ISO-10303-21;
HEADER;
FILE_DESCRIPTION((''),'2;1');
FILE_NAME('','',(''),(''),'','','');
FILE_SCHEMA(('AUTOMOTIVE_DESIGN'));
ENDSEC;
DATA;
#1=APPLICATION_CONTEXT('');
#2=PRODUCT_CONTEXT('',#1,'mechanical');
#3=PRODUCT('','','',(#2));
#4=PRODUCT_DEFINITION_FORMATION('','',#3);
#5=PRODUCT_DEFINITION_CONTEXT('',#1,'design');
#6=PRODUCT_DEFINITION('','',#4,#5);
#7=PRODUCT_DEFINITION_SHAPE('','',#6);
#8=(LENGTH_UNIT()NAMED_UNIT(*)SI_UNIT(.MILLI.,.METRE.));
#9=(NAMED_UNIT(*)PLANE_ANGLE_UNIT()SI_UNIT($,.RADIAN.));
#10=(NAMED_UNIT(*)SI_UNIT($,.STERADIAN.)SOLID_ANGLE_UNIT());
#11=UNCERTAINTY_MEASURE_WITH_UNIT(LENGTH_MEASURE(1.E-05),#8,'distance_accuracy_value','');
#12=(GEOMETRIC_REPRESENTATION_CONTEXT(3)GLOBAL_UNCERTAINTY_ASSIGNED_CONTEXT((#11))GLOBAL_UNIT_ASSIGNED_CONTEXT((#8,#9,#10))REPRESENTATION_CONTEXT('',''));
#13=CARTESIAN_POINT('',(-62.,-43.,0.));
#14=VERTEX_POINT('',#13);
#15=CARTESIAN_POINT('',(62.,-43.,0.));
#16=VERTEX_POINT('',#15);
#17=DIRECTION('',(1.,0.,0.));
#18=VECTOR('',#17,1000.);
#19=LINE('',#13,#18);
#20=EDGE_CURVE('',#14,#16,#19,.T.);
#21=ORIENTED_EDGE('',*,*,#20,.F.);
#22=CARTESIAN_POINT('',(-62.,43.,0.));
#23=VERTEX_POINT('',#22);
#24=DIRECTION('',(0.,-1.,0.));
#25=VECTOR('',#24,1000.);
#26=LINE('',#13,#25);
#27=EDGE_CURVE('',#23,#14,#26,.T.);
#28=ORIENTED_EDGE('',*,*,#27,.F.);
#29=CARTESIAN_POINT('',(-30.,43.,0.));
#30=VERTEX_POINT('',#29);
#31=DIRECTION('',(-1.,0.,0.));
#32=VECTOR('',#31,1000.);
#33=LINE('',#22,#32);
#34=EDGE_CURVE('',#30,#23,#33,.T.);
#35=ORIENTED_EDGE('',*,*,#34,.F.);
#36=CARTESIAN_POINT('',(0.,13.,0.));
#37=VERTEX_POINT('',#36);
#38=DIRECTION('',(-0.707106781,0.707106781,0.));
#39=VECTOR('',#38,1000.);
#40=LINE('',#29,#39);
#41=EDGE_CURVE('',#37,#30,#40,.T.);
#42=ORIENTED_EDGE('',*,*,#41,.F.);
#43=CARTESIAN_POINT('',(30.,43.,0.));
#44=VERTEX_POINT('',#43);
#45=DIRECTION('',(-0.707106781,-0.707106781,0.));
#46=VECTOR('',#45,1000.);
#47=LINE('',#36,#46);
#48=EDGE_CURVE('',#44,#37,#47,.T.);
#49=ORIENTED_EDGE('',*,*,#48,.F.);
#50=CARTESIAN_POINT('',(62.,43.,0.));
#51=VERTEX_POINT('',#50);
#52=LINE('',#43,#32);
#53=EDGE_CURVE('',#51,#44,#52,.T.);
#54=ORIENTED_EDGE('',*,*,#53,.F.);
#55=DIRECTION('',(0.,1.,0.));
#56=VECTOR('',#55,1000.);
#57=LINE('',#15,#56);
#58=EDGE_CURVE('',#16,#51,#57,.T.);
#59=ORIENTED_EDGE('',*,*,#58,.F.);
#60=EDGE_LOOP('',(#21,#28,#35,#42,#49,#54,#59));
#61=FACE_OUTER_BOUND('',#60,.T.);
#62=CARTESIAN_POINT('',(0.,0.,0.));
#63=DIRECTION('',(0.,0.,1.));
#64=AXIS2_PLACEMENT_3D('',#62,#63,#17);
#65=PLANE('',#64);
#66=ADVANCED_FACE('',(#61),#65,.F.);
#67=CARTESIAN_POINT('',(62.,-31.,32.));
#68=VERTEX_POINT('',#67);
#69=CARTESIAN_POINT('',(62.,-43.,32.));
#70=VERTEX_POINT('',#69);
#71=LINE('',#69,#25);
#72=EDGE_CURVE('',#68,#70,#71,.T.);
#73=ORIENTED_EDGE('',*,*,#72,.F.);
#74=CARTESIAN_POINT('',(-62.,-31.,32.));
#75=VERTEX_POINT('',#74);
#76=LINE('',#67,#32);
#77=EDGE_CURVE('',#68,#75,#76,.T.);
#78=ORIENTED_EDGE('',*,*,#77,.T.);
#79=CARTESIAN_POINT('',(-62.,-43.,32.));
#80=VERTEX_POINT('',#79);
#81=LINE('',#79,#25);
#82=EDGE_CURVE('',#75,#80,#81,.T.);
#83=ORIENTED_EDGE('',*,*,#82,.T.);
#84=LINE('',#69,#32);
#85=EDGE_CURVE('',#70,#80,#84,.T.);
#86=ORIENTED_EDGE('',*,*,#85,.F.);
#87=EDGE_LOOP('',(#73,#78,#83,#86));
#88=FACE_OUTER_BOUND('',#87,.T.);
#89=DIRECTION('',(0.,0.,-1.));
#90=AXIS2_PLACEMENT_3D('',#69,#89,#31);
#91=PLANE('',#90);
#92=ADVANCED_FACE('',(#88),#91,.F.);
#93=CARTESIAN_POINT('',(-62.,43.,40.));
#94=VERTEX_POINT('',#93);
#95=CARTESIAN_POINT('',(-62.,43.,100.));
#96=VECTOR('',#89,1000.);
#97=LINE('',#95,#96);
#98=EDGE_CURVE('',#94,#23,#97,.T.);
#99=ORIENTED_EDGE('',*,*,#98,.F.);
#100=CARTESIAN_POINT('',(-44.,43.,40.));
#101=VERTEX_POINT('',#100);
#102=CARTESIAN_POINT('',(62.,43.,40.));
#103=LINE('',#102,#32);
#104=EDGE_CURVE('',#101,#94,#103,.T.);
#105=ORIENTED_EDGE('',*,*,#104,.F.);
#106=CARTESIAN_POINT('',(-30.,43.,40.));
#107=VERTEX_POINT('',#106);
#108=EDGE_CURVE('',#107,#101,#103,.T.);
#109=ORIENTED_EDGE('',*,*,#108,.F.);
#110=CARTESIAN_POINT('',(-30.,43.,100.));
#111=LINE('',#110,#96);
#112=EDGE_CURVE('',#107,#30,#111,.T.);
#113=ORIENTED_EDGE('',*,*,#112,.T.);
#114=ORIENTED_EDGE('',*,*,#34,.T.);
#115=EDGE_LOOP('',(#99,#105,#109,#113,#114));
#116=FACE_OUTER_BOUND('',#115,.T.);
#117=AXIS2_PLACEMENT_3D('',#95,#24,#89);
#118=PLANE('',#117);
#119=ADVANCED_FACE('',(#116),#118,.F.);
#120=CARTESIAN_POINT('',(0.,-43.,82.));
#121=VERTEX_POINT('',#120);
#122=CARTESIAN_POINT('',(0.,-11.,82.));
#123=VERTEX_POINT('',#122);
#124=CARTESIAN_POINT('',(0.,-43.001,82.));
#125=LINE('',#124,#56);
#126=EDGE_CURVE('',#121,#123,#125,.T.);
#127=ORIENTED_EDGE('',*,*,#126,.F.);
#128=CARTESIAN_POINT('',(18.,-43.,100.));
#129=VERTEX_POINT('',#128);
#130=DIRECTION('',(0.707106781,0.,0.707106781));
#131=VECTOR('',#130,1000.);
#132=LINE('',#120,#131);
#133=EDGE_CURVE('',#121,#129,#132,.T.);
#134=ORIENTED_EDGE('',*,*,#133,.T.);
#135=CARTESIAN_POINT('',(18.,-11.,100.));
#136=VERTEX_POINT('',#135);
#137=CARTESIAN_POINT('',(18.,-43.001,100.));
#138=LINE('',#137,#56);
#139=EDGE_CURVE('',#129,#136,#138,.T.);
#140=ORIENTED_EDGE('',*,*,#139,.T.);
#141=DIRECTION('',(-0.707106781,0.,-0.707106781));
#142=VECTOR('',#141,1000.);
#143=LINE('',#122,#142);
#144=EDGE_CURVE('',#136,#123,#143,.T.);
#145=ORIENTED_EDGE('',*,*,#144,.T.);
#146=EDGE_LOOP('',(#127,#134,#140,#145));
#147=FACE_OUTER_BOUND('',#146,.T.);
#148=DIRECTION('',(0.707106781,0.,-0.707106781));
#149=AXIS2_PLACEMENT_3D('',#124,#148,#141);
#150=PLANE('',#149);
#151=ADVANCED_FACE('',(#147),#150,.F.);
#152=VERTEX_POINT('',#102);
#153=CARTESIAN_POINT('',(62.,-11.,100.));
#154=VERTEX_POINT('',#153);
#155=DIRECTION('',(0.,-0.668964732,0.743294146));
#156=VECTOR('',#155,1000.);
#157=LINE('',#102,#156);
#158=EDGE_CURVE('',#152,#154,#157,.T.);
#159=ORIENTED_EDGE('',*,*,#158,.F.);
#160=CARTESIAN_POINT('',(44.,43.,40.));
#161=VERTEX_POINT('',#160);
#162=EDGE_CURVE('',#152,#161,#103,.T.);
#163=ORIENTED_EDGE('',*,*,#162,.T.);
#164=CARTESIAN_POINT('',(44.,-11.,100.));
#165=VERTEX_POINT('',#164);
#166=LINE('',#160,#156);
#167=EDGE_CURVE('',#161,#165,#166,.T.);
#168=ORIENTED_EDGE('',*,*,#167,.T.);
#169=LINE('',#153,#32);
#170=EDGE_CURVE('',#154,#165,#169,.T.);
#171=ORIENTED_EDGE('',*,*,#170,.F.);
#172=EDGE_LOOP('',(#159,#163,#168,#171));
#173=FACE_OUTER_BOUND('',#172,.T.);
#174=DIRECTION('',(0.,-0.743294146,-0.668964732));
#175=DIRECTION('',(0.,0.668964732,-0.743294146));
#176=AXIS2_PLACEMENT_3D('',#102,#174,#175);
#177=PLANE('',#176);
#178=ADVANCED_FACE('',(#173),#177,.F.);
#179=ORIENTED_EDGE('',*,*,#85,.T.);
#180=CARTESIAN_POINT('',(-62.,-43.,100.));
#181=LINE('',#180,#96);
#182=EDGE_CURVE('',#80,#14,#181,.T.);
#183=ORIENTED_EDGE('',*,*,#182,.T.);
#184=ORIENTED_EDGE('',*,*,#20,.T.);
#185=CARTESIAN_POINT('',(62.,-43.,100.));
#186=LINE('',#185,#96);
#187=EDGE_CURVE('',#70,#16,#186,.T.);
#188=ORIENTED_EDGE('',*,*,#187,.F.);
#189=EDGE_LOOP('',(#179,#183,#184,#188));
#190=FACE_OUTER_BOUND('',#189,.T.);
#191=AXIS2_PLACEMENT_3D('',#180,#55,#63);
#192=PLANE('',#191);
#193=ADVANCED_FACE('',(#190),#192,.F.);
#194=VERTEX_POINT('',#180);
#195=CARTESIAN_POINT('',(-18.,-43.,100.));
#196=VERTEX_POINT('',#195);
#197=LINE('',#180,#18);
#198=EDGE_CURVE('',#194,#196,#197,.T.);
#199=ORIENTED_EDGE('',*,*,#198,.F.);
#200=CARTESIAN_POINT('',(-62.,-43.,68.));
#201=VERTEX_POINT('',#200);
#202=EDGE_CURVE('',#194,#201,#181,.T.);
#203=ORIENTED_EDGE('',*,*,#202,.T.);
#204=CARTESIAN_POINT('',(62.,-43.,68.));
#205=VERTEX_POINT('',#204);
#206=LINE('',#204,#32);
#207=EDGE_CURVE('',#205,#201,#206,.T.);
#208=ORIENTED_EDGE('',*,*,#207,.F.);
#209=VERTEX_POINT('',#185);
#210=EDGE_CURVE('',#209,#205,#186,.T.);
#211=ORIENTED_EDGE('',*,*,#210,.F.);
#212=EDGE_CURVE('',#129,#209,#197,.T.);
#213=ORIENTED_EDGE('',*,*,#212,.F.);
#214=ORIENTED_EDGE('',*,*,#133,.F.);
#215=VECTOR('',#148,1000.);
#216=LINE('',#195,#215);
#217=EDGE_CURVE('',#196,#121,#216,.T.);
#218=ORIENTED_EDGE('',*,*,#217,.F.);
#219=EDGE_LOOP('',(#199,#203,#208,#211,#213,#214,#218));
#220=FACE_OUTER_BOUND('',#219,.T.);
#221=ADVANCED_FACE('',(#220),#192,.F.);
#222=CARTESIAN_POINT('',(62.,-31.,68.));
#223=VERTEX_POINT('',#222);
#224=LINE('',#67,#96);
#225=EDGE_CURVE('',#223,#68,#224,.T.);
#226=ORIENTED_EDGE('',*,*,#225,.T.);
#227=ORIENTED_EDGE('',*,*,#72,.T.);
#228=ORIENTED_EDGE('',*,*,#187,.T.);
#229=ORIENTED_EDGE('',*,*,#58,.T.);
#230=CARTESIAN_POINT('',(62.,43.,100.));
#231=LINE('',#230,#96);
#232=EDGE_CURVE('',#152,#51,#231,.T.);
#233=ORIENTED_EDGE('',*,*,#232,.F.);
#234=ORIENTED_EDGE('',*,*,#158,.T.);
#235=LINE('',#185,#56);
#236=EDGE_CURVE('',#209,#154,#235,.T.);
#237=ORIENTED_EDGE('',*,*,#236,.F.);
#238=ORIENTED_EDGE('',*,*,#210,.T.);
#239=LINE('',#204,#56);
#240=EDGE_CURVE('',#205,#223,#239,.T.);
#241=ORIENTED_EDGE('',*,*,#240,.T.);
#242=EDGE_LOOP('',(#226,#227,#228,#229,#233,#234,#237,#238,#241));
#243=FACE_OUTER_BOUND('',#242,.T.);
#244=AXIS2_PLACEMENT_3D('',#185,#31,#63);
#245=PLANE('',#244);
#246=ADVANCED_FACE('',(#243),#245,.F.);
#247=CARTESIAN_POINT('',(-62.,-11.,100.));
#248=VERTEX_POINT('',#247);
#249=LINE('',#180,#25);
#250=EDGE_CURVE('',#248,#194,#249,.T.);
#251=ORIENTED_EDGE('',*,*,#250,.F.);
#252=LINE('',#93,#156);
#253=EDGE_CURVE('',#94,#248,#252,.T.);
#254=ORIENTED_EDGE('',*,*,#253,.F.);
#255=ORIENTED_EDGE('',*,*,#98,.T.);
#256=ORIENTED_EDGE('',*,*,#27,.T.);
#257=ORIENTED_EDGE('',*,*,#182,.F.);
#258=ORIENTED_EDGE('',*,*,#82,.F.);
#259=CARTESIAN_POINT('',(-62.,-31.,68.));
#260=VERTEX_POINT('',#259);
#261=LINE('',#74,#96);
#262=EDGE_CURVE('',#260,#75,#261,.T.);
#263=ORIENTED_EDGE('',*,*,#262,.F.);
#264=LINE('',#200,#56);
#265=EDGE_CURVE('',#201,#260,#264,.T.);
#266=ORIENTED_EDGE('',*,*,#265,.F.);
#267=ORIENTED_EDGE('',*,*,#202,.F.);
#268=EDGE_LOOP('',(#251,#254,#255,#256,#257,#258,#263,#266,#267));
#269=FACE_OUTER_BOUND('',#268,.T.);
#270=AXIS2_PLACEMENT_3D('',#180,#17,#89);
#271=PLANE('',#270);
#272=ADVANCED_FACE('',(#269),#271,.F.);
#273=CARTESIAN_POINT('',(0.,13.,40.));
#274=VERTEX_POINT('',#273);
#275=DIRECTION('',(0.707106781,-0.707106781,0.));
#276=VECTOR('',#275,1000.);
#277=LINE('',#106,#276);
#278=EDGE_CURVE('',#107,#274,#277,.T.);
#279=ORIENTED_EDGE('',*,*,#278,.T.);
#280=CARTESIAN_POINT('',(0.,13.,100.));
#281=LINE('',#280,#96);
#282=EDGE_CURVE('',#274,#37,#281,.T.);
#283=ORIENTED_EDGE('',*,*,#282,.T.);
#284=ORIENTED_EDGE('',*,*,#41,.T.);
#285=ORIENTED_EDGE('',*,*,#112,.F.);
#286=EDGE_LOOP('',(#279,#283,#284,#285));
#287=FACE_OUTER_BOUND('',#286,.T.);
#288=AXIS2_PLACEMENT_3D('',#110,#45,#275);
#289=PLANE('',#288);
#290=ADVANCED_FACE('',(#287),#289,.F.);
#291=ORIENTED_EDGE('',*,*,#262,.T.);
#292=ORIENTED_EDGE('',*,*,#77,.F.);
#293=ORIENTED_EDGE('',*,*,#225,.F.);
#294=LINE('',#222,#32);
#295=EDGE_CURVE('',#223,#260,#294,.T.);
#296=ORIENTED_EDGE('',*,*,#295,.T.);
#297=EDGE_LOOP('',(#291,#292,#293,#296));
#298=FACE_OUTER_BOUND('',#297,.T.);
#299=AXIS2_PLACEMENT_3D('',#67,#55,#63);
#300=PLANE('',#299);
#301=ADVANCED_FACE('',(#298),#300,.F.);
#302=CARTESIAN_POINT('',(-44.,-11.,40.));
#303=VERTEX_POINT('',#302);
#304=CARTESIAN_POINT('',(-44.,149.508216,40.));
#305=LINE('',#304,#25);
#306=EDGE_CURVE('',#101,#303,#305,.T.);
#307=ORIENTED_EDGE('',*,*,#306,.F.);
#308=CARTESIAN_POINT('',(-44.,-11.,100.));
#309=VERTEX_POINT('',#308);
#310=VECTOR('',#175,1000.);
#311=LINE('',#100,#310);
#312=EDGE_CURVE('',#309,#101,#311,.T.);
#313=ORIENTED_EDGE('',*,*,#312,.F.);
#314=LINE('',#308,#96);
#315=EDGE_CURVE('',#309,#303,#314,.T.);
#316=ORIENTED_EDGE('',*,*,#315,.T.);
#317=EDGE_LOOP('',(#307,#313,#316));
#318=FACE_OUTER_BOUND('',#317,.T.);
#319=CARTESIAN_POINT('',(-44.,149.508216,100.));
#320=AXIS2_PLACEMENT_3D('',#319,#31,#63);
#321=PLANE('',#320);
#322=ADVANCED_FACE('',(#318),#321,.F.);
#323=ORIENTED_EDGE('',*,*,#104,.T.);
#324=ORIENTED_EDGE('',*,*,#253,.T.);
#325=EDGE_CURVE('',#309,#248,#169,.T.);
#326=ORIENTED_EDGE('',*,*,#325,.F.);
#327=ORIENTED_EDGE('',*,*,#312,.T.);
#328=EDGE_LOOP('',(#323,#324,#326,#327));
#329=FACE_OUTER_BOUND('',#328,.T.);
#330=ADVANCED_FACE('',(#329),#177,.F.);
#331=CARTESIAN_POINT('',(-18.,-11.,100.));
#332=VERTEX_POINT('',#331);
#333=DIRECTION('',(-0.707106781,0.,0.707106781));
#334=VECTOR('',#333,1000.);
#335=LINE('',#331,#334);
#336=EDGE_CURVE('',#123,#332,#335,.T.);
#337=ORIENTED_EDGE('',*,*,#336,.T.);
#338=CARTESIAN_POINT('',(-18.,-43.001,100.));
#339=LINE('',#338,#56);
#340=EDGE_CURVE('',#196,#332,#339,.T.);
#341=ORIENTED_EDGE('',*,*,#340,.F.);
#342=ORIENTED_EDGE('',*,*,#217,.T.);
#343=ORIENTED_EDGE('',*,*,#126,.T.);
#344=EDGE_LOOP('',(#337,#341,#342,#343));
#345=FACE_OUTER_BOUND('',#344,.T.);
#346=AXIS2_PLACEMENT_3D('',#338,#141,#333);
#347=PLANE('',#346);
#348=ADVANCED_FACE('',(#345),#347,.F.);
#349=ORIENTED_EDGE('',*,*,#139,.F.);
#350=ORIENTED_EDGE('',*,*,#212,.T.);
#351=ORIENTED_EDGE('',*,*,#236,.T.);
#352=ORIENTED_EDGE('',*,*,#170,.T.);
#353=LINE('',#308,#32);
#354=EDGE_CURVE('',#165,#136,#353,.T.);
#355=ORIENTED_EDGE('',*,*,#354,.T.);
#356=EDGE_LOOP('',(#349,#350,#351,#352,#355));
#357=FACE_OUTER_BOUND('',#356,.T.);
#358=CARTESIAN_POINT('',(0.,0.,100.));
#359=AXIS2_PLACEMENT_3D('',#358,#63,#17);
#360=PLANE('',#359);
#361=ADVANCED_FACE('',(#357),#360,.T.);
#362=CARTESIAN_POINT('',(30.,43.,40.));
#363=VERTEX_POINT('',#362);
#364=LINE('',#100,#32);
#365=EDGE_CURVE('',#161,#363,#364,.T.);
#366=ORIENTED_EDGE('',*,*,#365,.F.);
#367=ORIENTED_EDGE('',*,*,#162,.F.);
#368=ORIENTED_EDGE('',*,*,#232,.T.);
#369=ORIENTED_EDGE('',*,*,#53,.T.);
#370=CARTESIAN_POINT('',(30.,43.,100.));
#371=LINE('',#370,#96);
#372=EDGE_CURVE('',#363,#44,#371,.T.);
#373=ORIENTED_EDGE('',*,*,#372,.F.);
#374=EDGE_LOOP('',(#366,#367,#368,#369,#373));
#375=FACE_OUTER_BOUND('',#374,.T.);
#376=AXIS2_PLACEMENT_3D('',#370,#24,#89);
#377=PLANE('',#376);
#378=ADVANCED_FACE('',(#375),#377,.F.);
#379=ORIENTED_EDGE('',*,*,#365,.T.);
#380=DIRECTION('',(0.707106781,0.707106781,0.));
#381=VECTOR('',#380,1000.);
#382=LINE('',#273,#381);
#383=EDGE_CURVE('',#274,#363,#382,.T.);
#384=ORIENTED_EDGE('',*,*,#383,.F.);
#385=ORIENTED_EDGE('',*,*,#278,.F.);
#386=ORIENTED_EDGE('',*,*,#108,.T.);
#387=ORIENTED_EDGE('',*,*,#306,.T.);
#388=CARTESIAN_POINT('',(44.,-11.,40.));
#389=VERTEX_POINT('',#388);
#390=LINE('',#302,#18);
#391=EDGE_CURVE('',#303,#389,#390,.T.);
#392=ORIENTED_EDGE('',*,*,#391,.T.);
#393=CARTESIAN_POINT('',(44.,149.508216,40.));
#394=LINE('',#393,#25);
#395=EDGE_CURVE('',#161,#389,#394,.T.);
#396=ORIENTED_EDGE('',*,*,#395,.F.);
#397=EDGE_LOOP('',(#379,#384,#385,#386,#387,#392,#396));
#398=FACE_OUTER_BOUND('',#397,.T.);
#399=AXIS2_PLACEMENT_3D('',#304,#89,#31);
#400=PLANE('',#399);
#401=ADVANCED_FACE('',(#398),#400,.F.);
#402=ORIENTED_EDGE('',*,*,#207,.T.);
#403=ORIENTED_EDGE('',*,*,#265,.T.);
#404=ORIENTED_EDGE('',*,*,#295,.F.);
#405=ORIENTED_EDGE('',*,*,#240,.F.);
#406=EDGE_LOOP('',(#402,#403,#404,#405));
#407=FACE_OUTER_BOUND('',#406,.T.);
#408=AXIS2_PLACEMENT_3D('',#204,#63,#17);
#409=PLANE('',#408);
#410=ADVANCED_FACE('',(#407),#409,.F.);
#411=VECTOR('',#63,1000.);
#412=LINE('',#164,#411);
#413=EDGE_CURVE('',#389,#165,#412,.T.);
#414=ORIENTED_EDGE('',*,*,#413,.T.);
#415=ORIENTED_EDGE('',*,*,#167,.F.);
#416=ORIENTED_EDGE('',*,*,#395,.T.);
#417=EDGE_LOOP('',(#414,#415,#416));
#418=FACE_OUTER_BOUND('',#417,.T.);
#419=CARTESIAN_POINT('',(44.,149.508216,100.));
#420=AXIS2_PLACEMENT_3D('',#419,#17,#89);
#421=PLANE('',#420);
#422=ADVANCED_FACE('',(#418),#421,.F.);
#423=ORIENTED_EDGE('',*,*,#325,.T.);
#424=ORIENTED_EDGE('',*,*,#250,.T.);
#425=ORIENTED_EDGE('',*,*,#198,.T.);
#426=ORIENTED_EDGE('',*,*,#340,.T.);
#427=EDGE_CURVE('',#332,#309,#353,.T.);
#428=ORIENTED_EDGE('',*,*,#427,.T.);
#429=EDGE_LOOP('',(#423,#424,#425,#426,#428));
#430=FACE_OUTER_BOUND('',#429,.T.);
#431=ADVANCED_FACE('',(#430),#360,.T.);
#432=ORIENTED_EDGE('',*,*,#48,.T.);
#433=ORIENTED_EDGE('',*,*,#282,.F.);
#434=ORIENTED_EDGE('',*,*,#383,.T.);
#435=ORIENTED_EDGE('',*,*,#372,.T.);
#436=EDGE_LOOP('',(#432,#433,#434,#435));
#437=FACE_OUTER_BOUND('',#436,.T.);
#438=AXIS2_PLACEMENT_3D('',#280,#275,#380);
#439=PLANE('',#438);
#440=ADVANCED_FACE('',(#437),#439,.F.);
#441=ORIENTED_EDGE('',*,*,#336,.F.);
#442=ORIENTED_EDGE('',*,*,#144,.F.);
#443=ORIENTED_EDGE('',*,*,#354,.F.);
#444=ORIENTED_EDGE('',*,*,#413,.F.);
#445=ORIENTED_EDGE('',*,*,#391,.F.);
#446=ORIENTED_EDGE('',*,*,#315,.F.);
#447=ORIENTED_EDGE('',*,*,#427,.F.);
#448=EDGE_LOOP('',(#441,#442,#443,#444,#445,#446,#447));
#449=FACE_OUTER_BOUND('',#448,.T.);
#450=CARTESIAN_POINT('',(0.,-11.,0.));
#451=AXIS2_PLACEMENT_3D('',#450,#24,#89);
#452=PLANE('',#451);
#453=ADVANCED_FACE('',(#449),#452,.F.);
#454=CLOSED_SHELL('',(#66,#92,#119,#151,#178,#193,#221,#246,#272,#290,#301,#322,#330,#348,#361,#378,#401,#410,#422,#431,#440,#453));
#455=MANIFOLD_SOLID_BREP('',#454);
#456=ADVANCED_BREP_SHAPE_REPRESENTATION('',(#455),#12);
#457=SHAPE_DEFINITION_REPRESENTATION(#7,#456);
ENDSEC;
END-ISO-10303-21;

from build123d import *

# Parameters (mm, degrees)
V_BLOCK_BODY_100_DEPTH    = 100
CENTRAL_CHANNEL_SKETCH_W  = 36
CENTRAL_CHANNEL_SKETCH_H  = 12
CENTRAL_CHANNEL_CUT_DEPTH = 166
SQUARE_POCKET_18X18_REACH = 179.739
SQUARE_START              = -32
SQUARE_POCKET_SKETCH_W    = 88
SQUARE_POCKET_SKETCH_H    = 60
ANGLED_NOTCH_CUT_REACH    = 131.46


with BuildPart() as part:
    # V-Block Profile Sketch → V-Block Body 100 (new body)
    with BuildSketch(Plane.XY):
        Polygon((-30, 43), (0, 13), (30, 43), (62, 43), (62, -43), (-62, -43), (-62, 43), align=None)
    extrude(amount=V_BLOCK_BODY_100_DEPTH)

    # Central Channel Sketch → Central Channel Cut (cut, through all)
    with BuildSketch(Plane.ZY.offset(62)):
        with Locations((50, -37)):
            Rectangle(CENTRAL_CHANNEL_SKETCH_W, CENTRAL_CHANNEL_SKETCH_H)
        Polygon((40, 43), (100, -11), (100, 43), align=None)
    extrude(amount=-CENTRAL_CHANNEL_CUT_DEPTH, mode=Mode.SUBTRACT)

    # Square Pocket 18x18: up to this face of the body (flat: up to its plane)
    square_pocket_18x18_end = Plane(part.part.faces().sort_by_distance((-46, 43, 20))[0])
    # Square Pocket Sketch → Square Pocket 18x18 (cut, up to the picked face)
    with BuildSketch(Plane.XZ.offset(43).offset(SQUARE_START), mode=Mode.PRIVATE) as square_pocket_18x18_sk1:
        with Locations((0, 70)):
            Rectangle(SQUARE_POCKET_SKETCH_W, SQUARE_POCKET_SKETCH_H)
    square_pocket_18x18_tool1 = split(extrude(square_pocket_18x18_sk1.sketch, amount=-SQUARE_POCKET_18X18_REACH, mode=Mode.PRIVATE), bisect_by=square_pocket_18x18_end, keep=Keep.BOTH, mode=Mode.PRIVATE)
    add(square_pocket_18x18_tool1.solids().sort_by(Axis((0, -11, 70), (0, 1, 0)))[0], mode=Mode.SUBTRACT)

    # Angled Notch Sketch → Angled Notch Cut (cut, up to next)
    with BuildSketch(Plane(origin=(0, -11, 0), x_dir=(1, 0, 0), z_dir=(0, 1, 0)), mode=Mode.PRIVATE) as angled_notch_cut_sk1:
        Polygon((-18, -100), (0, -82), (18, -100), align=None)
    angled_notch_cut_tool1 = extrude(angled_notch_cut_sk1.sketch, amount=-ANGLED_NOTCH_CUT_REACH, mode=Mode.PRIVATE) & part.part
    add(angled_notch_cut_tool1.solids().sort_by_distance((0, -11, 94))[0], mode=Mode.SUBTRACT)


solid = part.part
